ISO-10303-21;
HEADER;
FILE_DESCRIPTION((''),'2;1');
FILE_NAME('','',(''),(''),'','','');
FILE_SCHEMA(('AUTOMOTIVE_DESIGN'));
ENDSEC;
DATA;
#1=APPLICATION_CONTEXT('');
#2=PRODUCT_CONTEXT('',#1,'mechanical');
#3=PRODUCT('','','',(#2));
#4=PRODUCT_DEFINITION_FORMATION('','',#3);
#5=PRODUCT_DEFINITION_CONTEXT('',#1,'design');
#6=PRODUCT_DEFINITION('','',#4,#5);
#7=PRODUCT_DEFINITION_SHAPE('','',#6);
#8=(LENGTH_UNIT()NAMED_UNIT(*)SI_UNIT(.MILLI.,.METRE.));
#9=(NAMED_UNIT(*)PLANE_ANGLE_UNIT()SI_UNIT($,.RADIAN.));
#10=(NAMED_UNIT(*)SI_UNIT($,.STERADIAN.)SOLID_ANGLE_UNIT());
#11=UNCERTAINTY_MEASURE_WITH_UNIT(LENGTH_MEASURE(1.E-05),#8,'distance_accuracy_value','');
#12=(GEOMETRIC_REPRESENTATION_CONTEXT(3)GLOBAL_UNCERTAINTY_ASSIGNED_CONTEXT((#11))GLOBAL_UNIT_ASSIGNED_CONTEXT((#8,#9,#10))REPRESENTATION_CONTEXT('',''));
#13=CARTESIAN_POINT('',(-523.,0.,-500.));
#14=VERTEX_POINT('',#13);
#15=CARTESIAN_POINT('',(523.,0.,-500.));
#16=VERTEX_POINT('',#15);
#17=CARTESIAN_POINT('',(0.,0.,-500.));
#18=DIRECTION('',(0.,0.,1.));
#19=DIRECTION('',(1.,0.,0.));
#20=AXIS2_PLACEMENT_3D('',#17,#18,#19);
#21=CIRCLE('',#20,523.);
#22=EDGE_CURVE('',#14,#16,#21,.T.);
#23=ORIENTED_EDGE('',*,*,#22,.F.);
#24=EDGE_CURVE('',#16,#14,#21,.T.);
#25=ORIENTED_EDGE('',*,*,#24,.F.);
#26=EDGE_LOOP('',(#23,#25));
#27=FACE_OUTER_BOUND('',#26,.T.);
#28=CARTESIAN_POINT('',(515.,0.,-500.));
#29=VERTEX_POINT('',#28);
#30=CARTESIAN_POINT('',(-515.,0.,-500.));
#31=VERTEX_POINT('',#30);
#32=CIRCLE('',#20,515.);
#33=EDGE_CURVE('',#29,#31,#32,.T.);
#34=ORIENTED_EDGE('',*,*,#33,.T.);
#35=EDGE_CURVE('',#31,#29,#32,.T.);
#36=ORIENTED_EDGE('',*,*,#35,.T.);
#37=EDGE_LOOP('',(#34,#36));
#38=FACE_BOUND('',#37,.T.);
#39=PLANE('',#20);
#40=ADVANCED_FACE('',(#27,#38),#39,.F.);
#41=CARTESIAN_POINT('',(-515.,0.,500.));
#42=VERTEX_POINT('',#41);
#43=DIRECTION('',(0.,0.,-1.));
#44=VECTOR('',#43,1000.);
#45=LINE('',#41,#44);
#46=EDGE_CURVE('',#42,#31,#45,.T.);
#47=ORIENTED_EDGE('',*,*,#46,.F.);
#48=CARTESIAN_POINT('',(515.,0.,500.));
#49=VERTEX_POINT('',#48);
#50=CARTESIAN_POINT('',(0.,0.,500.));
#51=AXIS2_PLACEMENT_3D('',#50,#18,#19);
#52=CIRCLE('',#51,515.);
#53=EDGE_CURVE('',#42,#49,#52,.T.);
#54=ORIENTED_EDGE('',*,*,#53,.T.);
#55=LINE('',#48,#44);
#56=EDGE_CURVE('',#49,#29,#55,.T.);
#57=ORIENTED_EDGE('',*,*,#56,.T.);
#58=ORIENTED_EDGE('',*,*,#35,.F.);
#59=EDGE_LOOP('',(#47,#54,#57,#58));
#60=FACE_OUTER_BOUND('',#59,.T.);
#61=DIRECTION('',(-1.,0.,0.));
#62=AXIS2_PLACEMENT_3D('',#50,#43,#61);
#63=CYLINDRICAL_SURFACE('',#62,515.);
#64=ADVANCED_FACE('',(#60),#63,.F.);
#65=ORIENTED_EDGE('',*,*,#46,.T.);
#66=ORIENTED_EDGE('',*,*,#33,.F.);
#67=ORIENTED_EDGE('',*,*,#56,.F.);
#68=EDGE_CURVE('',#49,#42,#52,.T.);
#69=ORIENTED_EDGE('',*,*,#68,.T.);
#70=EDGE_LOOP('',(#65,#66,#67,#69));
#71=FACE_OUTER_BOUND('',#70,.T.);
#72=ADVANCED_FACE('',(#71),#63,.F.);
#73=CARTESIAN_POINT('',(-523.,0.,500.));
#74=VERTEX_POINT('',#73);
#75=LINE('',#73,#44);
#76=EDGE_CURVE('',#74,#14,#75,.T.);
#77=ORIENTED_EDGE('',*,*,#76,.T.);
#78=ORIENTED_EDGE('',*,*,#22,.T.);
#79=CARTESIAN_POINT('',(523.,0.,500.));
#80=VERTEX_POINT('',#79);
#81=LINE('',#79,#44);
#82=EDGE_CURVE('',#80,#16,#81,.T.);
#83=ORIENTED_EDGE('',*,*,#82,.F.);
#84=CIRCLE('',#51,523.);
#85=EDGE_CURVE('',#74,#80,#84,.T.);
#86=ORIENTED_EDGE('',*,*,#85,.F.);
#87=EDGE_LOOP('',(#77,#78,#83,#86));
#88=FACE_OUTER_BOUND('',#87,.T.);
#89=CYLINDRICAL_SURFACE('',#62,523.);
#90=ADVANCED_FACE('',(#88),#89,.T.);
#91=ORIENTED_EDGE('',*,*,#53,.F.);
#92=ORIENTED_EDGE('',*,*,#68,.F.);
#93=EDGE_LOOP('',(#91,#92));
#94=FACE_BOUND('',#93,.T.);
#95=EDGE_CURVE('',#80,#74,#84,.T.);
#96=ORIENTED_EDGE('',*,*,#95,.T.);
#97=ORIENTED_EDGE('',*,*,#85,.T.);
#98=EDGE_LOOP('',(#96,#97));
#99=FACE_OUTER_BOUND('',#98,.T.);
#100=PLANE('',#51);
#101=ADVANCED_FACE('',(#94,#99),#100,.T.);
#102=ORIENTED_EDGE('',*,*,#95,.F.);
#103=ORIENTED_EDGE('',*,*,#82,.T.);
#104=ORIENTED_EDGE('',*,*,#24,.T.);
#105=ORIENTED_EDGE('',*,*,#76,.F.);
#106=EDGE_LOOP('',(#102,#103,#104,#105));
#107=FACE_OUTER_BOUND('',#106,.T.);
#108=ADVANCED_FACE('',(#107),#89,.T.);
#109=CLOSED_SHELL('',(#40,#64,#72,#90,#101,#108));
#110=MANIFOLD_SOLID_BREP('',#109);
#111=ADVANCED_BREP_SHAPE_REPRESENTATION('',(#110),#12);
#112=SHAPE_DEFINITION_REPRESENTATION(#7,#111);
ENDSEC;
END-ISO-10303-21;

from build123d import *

# Parameters (mm, degrees)
SKETCH1_R           = 523
SKETCH1_R_2         = 515
EXTRUDE_THIN1_DEPTH = 500


with BuildPart() as part:
    # Sketch1 → Extrude-Thin1 (new, symmetric)
    with BuildSketch(Plane.XY):
        Circle(SKETCH1_R)
        Circle(SKETCH1_R_2, mode=Mode.SUBTRACT)
    extrude(amount=EXTRUDE_THIN1_DEPTH, both=True)


solid = part.part
